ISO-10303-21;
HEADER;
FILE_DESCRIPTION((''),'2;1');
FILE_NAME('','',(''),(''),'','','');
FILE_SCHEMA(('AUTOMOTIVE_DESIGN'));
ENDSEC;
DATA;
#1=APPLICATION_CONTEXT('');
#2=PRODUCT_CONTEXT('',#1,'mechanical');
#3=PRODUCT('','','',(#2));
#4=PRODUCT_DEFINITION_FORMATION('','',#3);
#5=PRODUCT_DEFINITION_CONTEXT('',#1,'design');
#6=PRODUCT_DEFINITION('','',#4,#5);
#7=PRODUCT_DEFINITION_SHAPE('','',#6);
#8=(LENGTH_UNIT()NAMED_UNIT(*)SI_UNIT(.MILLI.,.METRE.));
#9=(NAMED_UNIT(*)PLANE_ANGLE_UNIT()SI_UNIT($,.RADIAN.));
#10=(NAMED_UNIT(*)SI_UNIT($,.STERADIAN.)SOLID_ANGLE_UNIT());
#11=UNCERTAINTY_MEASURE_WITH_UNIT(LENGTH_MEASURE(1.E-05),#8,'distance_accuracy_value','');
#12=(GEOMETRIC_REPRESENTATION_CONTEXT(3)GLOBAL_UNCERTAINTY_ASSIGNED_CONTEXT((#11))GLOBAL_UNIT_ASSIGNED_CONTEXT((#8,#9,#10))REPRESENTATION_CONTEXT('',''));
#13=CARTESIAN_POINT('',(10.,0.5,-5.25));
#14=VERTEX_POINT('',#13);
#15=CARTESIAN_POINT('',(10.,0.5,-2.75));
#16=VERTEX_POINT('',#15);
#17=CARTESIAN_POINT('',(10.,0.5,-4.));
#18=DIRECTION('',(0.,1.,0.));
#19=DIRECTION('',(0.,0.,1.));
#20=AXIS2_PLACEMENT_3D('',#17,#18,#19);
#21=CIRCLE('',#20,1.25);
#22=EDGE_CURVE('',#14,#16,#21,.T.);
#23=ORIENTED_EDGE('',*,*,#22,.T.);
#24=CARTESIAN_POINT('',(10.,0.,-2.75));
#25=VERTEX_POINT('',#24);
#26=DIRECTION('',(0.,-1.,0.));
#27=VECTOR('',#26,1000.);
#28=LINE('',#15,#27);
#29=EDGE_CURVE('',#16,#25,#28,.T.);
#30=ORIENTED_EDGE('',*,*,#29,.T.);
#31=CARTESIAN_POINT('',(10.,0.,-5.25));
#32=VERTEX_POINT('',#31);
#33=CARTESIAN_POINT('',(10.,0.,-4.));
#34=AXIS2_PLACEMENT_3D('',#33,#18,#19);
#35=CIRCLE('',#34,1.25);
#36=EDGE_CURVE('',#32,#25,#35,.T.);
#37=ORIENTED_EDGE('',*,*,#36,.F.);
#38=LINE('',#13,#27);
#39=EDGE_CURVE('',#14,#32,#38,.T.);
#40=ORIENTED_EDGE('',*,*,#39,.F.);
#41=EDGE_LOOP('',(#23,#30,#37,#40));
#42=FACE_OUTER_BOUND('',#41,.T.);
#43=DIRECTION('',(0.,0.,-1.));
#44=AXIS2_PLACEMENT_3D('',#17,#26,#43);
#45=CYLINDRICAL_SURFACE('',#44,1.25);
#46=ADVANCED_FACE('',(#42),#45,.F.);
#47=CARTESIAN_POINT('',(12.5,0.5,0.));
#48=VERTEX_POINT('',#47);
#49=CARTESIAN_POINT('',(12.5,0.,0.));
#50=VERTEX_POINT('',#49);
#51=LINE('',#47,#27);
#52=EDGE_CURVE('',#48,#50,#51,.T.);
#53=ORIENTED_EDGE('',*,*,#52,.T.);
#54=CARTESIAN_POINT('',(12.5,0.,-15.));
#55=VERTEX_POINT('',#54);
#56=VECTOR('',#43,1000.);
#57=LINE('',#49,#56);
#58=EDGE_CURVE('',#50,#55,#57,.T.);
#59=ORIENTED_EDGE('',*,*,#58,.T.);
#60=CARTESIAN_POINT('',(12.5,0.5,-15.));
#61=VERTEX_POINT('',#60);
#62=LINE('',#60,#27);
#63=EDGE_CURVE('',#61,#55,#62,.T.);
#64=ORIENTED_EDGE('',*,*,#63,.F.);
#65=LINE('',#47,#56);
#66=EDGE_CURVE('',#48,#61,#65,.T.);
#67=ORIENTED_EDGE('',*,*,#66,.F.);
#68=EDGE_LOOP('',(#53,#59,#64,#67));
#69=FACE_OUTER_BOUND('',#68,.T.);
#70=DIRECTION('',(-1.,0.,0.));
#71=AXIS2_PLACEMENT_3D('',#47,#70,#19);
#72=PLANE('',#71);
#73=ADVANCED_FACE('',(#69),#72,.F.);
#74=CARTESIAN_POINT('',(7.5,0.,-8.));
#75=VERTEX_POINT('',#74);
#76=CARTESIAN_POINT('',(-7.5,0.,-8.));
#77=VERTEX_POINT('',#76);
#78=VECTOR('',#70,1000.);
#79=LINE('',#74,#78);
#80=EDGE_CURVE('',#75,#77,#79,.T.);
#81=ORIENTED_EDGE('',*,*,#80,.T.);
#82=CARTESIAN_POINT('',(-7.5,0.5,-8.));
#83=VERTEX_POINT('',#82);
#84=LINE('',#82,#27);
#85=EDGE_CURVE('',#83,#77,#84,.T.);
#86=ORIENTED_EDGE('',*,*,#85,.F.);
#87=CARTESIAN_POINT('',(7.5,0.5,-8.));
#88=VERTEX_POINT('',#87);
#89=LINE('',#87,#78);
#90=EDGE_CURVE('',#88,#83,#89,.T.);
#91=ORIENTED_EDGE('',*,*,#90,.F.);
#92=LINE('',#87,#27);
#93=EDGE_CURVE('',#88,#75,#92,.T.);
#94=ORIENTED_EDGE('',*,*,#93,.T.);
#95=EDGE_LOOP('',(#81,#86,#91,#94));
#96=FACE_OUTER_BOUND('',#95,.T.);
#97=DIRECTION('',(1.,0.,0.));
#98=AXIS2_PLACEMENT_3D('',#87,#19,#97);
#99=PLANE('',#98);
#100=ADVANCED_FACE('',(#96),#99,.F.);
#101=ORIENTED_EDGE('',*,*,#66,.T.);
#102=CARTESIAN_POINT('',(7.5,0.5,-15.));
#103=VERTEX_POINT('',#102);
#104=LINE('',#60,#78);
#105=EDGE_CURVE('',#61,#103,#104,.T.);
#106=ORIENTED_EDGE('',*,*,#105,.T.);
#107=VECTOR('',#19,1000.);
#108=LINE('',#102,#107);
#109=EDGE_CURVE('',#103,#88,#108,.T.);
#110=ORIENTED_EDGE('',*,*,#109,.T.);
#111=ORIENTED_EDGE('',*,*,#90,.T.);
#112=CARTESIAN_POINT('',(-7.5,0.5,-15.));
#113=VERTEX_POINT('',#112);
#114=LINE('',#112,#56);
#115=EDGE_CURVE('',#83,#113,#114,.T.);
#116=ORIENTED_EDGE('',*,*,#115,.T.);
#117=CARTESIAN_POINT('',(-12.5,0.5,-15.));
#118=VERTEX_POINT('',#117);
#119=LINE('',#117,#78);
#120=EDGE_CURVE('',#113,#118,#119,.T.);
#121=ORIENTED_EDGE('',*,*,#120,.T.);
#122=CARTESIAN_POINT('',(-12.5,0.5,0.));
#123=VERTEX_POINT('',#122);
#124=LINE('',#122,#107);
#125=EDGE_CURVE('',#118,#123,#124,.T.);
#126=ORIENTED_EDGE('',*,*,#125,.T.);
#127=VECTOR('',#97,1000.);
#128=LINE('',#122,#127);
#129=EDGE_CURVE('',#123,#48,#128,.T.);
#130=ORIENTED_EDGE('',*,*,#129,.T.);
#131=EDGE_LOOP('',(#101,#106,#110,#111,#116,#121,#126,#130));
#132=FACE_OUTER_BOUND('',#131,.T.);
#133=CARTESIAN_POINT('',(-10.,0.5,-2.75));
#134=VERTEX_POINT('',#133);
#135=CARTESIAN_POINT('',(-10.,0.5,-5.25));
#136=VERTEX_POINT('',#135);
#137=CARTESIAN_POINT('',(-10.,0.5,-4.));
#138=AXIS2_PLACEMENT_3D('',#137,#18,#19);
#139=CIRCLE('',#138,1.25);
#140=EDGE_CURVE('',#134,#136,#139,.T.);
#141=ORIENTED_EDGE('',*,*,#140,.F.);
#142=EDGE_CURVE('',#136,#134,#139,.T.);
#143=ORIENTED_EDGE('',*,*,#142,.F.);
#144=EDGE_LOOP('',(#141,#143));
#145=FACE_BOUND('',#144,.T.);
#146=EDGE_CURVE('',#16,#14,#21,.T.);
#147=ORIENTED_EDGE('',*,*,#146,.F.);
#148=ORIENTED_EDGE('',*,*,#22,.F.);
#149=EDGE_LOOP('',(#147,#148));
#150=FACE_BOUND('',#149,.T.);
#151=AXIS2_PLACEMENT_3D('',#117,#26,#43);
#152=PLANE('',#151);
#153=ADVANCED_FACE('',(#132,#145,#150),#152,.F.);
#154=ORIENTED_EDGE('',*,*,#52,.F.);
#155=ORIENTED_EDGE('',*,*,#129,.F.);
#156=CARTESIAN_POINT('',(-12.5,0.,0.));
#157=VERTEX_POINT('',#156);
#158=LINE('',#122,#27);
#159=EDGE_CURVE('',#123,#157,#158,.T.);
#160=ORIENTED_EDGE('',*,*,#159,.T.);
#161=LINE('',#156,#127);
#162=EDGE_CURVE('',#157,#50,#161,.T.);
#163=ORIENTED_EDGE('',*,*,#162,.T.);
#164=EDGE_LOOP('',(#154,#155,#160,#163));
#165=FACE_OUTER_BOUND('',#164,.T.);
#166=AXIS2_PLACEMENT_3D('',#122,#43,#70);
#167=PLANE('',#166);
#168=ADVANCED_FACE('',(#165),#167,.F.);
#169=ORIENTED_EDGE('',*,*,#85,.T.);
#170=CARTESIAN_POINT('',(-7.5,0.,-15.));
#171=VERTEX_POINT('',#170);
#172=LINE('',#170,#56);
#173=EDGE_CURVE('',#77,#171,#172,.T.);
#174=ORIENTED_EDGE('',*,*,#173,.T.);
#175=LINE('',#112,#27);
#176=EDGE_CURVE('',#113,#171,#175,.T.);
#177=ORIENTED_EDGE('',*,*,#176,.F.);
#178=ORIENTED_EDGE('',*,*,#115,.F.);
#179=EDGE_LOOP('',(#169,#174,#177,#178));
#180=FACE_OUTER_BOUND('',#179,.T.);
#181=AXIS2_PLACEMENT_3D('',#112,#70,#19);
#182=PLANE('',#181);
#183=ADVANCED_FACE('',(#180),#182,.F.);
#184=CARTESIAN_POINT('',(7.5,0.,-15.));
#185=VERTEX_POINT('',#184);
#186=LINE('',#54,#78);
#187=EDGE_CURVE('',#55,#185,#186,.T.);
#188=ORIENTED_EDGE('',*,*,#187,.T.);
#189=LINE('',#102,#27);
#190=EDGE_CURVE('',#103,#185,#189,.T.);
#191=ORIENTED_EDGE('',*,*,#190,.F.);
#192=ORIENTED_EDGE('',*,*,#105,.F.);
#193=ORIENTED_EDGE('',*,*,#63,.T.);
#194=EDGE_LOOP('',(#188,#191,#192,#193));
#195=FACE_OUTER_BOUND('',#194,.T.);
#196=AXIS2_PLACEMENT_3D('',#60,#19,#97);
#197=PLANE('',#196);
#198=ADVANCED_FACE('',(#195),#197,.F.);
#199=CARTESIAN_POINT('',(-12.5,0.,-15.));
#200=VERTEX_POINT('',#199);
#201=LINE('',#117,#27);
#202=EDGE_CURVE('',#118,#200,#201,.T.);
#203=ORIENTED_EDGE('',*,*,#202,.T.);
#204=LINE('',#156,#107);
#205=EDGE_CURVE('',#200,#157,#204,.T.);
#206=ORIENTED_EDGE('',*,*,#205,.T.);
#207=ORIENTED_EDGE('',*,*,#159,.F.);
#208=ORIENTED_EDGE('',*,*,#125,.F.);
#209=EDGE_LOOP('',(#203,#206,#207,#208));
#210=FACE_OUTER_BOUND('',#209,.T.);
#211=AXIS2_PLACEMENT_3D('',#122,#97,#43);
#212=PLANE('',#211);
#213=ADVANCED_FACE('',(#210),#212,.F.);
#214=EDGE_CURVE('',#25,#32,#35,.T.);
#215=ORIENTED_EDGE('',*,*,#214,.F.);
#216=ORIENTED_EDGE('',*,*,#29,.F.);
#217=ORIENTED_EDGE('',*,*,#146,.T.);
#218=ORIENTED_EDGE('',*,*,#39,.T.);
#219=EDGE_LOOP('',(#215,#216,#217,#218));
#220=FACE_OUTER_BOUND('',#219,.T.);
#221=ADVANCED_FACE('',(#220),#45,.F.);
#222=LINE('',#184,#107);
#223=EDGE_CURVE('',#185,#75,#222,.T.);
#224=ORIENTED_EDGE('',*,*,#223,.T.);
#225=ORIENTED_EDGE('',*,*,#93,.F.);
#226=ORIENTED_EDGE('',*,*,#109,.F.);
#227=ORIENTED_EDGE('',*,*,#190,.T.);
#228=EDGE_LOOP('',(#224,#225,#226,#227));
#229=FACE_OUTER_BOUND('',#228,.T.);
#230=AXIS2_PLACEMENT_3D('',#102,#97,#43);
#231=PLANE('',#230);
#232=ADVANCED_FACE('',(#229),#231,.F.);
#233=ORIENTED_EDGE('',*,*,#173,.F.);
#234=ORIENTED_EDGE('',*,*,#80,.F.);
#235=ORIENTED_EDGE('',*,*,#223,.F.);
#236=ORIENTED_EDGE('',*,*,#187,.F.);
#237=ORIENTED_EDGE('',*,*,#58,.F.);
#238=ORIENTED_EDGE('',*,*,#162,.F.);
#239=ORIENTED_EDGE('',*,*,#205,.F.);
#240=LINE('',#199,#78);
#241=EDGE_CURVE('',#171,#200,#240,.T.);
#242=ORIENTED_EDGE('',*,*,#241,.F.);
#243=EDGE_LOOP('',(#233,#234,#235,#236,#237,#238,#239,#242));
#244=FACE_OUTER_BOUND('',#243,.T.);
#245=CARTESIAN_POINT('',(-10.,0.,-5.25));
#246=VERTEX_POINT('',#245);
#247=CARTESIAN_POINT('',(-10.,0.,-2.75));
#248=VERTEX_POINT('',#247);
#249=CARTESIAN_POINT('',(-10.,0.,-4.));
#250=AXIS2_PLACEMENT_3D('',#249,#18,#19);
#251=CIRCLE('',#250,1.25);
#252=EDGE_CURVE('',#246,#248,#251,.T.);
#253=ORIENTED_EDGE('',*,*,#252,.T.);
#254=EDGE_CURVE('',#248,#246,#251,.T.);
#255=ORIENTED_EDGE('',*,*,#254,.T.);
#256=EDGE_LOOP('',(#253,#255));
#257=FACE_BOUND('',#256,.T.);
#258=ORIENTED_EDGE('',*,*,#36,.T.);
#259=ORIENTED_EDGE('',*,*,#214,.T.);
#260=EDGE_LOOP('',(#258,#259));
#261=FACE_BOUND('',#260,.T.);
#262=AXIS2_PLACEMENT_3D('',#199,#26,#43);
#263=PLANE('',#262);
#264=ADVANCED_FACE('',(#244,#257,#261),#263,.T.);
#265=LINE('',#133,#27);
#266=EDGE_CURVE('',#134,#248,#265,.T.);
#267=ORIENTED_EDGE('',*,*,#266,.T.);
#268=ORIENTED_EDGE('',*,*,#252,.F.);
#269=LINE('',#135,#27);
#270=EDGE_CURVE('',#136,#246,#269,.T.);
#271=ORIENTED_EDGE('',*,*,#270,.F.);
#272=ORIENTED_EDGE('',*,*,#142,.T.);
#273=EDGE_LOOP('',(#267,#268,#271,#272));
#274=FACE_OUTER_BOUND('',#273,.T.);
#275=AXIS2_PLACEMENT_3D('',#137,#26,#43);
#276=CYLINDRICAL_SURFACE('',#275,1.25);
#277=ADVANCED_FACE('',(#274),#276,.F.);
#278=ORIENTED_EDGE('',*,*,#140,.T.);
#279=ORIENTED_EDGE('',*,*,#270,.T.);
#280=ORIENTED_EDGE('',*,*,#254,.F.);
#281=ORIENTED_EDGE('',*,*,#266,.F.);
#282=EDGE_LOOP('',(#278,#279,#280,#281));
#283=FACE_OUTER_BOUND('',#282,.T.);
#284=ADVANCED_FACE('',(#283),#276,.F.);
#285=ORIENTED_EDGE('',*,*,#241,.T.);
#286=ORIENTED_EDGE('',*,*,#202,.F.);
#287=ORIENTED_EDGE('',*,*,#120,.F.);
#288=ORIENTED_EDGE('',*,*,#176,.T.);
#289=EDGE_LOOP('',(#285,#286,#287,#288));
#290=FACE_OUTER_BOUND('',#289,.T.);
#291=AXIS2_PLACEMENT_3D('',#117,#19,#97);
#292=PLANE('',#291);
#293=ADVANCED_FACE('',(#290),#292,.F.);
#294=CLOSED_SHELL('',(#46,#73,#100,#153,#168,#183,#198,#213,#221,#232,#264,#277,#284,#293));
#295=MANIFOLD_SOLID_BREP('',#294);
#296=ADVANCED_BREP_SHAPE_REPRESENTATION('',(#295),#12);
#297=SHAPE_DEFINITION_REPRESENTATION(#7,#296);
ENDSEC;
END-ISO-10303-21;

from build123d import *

# Parameters (mm, degrees)
SKETCH1_R           = 1.25
BOSS_EXTRUDE1_DEPTH = 0.5


with BuildPart() as part:
    # Sketch1 → Boss-Extrude1 (new body)
    with BuildSketch(Plane(origin=(0, 0, 0), x_dir=(1, 0, 0), z_dir=(0, 1, 0))):
        Polygon((-12.5, 0), (12.5, 0), (12.5, 15), (7.5, 15), (7.5, 8), (-7.5, 8), (-7.5, 15), (-12.5, 15), align=None)
        with Locations(Location((10, 4, 0), (0, 0, 270))):
            Circle(SKETCH1_R, mode=Mode.SUBTRACT)
        with Locations(Location((-10, 4, 0), (0, 0, 270))):
            Circle(SKETCH1_R, mode=Mode.SUBTRACT)
    extrude(amount=BOSS_EXTRUDE1_DEPTH)


solid = part.part
